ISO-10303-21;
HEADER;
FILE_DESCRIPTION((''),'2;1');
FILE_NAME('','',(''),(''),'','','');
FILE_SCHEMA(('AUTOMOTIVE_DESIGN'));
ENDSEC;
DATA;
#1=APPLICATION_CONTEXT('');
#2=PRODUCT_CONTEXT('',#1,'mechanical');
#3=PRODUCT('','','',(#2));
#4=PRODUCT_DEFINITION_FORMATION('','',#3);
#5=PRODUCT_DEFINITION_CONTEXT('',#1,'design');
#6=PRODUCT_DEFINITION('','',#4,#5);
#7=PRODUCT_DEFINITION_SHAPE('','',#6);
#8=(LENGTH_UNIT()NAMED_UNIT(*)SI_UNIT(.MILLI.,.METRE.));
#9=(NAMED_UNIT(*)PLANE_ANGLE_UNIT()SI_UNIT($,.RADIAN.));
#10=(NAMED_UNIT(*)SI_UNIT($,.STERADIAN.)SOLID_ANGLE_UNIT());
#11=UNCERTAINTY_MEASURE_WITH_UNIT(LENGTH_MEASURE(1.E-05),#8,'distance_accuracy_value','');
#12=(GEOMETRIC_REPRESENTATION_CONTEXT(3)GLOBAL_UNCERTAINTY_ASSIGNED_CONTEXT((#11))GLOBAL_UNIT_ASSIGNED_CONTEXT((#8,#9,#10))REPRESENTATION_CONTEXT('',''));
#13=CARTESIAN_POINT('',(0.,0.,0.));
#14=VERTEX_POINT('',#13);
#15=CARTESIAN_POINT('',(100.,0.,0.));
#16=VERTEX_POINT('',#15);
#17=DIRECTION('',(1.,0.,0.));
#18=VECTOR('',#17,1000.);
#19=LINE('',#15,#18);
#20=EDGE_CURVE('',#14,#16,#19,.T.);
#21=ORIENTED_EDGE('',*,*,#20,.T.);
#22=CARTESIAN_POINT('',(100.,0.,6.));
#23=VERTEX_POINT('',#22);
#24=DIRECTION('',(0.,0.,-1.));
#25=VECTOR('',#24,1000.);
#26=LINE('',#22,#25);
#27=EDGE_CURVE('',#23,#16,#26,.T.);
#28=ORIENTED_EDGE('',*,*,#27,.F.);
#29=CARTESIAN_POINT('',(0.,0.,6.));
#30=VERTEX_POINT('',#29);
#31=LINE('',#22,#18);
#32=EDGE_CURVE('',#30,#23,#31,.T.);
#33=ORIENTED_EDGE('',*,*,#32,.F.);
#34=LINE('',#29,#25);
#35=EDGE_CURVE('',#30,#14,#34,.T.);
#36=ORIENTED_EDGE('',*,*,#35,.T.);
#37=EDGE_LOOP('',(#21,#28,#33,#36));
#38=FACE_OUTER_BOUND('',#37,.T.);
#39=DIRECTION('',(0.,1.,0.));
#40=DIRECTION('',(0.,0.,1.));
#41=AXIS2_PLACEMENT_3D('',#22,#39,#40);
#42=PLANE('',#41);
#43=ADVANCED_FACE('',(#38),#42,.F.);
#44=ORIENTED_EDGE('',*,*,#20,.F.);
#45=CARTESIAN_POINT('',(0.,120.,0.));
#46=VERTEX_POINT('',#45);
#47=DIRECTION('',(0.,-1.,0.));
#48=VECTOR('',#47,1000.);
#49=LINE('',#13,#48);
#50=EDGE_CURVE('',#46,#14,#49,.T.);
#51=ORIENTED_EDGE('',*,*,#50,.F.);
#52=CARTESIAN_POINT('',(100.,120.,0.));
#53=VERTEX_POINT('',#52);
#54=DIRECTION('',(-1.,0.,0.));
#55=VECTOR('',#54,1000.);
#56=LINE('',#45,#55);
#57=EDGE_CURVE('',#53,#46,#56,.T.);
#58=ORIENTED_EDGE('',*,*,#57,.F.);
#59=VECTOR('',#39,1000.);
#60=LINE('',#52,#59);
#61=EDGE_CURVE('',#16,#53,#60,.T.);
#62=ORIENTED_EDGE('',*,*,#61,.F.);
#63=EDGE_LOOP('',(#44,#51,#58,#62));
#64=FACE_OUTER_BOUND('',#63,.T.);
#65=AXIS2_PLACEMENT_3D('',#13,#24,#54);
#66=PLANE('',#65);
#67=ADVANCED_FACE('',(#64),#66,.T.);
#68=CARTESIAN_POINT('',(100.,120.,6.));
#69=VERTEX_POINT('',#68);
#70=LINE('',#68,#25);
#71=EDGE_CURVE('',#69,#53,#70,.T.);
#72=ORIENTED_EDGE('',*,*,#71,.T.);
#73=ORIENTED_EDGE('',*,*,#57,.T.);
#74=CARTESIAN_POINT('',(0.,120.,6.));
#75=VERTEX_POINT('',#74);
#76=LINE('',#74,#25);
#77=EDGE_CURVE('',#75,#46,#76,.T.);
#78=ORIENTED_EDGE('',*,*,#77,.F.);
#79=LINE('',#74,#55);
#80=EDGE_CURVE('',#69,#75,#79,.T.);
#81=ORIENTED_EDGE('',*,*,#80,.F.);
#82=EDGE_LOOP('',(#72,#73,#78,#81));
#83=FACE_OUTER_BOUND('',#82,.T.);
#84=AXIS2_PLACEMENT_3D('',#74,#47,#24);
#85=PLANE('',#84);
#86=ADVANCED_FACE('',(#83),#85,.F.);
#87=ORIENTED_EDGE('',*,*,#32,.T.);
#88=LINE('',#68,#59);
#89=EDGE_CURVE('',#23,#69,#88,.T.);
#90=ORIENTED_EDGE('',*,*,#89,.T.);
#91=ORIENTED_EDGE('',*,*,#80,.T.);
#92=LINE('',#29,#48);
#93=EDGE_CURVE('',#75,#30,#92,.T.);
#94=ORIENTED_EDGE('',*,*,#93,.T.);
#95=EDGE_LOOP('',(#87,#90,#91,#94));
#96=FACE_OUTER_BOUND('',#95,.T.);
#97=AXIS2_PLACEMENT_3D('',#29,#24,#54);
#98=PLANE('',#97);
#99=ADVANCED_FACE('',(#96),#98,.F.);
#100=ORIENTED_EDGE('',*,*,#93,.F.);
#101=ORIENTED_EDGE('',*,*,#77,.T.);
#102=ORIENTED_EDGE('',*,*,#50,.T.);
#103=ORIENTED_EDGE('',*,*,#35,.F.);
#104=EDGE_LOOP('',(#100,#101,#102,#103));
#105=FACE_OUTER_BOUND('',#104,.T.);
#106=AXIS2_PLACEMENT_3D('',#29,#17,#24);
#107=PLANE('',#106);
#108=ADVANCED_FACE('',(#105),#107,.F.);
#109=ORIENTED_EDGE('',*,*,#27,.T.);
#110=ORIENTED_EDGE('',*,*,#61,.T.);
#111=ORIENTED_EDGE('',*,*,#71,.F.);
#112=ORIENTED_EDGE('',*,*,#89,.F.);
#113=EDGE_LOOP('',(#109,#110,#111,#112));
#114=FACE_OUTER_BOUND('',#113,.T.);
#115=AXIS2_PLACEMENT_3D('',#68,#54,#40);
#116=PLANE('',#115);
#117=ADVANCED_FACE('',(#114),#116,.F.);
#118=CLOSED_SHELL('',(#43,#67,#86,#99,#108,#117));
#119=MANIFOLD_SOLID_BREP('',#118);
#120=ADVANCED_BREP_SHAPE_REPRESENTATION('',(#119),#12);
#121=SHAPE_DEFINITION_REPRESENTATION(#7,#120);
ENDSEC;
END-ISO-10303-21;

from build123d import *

# Parameters (mm, degrees)
SKETCH_1_W      = 100
SKETCH_1_H      = 120
EXTRUDE_1_DEPTH = 6


with BuildPart() as part:
    # 草图1 → 凸台-拉伸1 (new body)
    with BuildSketch(Plane.XY):
        with Locations((50, 60)):
            Rectangle(SKETCH_1_W, SKETCH_1_H)
    extrude(amount=EXTRUDE_1_DEPTH)


solid = part.part
